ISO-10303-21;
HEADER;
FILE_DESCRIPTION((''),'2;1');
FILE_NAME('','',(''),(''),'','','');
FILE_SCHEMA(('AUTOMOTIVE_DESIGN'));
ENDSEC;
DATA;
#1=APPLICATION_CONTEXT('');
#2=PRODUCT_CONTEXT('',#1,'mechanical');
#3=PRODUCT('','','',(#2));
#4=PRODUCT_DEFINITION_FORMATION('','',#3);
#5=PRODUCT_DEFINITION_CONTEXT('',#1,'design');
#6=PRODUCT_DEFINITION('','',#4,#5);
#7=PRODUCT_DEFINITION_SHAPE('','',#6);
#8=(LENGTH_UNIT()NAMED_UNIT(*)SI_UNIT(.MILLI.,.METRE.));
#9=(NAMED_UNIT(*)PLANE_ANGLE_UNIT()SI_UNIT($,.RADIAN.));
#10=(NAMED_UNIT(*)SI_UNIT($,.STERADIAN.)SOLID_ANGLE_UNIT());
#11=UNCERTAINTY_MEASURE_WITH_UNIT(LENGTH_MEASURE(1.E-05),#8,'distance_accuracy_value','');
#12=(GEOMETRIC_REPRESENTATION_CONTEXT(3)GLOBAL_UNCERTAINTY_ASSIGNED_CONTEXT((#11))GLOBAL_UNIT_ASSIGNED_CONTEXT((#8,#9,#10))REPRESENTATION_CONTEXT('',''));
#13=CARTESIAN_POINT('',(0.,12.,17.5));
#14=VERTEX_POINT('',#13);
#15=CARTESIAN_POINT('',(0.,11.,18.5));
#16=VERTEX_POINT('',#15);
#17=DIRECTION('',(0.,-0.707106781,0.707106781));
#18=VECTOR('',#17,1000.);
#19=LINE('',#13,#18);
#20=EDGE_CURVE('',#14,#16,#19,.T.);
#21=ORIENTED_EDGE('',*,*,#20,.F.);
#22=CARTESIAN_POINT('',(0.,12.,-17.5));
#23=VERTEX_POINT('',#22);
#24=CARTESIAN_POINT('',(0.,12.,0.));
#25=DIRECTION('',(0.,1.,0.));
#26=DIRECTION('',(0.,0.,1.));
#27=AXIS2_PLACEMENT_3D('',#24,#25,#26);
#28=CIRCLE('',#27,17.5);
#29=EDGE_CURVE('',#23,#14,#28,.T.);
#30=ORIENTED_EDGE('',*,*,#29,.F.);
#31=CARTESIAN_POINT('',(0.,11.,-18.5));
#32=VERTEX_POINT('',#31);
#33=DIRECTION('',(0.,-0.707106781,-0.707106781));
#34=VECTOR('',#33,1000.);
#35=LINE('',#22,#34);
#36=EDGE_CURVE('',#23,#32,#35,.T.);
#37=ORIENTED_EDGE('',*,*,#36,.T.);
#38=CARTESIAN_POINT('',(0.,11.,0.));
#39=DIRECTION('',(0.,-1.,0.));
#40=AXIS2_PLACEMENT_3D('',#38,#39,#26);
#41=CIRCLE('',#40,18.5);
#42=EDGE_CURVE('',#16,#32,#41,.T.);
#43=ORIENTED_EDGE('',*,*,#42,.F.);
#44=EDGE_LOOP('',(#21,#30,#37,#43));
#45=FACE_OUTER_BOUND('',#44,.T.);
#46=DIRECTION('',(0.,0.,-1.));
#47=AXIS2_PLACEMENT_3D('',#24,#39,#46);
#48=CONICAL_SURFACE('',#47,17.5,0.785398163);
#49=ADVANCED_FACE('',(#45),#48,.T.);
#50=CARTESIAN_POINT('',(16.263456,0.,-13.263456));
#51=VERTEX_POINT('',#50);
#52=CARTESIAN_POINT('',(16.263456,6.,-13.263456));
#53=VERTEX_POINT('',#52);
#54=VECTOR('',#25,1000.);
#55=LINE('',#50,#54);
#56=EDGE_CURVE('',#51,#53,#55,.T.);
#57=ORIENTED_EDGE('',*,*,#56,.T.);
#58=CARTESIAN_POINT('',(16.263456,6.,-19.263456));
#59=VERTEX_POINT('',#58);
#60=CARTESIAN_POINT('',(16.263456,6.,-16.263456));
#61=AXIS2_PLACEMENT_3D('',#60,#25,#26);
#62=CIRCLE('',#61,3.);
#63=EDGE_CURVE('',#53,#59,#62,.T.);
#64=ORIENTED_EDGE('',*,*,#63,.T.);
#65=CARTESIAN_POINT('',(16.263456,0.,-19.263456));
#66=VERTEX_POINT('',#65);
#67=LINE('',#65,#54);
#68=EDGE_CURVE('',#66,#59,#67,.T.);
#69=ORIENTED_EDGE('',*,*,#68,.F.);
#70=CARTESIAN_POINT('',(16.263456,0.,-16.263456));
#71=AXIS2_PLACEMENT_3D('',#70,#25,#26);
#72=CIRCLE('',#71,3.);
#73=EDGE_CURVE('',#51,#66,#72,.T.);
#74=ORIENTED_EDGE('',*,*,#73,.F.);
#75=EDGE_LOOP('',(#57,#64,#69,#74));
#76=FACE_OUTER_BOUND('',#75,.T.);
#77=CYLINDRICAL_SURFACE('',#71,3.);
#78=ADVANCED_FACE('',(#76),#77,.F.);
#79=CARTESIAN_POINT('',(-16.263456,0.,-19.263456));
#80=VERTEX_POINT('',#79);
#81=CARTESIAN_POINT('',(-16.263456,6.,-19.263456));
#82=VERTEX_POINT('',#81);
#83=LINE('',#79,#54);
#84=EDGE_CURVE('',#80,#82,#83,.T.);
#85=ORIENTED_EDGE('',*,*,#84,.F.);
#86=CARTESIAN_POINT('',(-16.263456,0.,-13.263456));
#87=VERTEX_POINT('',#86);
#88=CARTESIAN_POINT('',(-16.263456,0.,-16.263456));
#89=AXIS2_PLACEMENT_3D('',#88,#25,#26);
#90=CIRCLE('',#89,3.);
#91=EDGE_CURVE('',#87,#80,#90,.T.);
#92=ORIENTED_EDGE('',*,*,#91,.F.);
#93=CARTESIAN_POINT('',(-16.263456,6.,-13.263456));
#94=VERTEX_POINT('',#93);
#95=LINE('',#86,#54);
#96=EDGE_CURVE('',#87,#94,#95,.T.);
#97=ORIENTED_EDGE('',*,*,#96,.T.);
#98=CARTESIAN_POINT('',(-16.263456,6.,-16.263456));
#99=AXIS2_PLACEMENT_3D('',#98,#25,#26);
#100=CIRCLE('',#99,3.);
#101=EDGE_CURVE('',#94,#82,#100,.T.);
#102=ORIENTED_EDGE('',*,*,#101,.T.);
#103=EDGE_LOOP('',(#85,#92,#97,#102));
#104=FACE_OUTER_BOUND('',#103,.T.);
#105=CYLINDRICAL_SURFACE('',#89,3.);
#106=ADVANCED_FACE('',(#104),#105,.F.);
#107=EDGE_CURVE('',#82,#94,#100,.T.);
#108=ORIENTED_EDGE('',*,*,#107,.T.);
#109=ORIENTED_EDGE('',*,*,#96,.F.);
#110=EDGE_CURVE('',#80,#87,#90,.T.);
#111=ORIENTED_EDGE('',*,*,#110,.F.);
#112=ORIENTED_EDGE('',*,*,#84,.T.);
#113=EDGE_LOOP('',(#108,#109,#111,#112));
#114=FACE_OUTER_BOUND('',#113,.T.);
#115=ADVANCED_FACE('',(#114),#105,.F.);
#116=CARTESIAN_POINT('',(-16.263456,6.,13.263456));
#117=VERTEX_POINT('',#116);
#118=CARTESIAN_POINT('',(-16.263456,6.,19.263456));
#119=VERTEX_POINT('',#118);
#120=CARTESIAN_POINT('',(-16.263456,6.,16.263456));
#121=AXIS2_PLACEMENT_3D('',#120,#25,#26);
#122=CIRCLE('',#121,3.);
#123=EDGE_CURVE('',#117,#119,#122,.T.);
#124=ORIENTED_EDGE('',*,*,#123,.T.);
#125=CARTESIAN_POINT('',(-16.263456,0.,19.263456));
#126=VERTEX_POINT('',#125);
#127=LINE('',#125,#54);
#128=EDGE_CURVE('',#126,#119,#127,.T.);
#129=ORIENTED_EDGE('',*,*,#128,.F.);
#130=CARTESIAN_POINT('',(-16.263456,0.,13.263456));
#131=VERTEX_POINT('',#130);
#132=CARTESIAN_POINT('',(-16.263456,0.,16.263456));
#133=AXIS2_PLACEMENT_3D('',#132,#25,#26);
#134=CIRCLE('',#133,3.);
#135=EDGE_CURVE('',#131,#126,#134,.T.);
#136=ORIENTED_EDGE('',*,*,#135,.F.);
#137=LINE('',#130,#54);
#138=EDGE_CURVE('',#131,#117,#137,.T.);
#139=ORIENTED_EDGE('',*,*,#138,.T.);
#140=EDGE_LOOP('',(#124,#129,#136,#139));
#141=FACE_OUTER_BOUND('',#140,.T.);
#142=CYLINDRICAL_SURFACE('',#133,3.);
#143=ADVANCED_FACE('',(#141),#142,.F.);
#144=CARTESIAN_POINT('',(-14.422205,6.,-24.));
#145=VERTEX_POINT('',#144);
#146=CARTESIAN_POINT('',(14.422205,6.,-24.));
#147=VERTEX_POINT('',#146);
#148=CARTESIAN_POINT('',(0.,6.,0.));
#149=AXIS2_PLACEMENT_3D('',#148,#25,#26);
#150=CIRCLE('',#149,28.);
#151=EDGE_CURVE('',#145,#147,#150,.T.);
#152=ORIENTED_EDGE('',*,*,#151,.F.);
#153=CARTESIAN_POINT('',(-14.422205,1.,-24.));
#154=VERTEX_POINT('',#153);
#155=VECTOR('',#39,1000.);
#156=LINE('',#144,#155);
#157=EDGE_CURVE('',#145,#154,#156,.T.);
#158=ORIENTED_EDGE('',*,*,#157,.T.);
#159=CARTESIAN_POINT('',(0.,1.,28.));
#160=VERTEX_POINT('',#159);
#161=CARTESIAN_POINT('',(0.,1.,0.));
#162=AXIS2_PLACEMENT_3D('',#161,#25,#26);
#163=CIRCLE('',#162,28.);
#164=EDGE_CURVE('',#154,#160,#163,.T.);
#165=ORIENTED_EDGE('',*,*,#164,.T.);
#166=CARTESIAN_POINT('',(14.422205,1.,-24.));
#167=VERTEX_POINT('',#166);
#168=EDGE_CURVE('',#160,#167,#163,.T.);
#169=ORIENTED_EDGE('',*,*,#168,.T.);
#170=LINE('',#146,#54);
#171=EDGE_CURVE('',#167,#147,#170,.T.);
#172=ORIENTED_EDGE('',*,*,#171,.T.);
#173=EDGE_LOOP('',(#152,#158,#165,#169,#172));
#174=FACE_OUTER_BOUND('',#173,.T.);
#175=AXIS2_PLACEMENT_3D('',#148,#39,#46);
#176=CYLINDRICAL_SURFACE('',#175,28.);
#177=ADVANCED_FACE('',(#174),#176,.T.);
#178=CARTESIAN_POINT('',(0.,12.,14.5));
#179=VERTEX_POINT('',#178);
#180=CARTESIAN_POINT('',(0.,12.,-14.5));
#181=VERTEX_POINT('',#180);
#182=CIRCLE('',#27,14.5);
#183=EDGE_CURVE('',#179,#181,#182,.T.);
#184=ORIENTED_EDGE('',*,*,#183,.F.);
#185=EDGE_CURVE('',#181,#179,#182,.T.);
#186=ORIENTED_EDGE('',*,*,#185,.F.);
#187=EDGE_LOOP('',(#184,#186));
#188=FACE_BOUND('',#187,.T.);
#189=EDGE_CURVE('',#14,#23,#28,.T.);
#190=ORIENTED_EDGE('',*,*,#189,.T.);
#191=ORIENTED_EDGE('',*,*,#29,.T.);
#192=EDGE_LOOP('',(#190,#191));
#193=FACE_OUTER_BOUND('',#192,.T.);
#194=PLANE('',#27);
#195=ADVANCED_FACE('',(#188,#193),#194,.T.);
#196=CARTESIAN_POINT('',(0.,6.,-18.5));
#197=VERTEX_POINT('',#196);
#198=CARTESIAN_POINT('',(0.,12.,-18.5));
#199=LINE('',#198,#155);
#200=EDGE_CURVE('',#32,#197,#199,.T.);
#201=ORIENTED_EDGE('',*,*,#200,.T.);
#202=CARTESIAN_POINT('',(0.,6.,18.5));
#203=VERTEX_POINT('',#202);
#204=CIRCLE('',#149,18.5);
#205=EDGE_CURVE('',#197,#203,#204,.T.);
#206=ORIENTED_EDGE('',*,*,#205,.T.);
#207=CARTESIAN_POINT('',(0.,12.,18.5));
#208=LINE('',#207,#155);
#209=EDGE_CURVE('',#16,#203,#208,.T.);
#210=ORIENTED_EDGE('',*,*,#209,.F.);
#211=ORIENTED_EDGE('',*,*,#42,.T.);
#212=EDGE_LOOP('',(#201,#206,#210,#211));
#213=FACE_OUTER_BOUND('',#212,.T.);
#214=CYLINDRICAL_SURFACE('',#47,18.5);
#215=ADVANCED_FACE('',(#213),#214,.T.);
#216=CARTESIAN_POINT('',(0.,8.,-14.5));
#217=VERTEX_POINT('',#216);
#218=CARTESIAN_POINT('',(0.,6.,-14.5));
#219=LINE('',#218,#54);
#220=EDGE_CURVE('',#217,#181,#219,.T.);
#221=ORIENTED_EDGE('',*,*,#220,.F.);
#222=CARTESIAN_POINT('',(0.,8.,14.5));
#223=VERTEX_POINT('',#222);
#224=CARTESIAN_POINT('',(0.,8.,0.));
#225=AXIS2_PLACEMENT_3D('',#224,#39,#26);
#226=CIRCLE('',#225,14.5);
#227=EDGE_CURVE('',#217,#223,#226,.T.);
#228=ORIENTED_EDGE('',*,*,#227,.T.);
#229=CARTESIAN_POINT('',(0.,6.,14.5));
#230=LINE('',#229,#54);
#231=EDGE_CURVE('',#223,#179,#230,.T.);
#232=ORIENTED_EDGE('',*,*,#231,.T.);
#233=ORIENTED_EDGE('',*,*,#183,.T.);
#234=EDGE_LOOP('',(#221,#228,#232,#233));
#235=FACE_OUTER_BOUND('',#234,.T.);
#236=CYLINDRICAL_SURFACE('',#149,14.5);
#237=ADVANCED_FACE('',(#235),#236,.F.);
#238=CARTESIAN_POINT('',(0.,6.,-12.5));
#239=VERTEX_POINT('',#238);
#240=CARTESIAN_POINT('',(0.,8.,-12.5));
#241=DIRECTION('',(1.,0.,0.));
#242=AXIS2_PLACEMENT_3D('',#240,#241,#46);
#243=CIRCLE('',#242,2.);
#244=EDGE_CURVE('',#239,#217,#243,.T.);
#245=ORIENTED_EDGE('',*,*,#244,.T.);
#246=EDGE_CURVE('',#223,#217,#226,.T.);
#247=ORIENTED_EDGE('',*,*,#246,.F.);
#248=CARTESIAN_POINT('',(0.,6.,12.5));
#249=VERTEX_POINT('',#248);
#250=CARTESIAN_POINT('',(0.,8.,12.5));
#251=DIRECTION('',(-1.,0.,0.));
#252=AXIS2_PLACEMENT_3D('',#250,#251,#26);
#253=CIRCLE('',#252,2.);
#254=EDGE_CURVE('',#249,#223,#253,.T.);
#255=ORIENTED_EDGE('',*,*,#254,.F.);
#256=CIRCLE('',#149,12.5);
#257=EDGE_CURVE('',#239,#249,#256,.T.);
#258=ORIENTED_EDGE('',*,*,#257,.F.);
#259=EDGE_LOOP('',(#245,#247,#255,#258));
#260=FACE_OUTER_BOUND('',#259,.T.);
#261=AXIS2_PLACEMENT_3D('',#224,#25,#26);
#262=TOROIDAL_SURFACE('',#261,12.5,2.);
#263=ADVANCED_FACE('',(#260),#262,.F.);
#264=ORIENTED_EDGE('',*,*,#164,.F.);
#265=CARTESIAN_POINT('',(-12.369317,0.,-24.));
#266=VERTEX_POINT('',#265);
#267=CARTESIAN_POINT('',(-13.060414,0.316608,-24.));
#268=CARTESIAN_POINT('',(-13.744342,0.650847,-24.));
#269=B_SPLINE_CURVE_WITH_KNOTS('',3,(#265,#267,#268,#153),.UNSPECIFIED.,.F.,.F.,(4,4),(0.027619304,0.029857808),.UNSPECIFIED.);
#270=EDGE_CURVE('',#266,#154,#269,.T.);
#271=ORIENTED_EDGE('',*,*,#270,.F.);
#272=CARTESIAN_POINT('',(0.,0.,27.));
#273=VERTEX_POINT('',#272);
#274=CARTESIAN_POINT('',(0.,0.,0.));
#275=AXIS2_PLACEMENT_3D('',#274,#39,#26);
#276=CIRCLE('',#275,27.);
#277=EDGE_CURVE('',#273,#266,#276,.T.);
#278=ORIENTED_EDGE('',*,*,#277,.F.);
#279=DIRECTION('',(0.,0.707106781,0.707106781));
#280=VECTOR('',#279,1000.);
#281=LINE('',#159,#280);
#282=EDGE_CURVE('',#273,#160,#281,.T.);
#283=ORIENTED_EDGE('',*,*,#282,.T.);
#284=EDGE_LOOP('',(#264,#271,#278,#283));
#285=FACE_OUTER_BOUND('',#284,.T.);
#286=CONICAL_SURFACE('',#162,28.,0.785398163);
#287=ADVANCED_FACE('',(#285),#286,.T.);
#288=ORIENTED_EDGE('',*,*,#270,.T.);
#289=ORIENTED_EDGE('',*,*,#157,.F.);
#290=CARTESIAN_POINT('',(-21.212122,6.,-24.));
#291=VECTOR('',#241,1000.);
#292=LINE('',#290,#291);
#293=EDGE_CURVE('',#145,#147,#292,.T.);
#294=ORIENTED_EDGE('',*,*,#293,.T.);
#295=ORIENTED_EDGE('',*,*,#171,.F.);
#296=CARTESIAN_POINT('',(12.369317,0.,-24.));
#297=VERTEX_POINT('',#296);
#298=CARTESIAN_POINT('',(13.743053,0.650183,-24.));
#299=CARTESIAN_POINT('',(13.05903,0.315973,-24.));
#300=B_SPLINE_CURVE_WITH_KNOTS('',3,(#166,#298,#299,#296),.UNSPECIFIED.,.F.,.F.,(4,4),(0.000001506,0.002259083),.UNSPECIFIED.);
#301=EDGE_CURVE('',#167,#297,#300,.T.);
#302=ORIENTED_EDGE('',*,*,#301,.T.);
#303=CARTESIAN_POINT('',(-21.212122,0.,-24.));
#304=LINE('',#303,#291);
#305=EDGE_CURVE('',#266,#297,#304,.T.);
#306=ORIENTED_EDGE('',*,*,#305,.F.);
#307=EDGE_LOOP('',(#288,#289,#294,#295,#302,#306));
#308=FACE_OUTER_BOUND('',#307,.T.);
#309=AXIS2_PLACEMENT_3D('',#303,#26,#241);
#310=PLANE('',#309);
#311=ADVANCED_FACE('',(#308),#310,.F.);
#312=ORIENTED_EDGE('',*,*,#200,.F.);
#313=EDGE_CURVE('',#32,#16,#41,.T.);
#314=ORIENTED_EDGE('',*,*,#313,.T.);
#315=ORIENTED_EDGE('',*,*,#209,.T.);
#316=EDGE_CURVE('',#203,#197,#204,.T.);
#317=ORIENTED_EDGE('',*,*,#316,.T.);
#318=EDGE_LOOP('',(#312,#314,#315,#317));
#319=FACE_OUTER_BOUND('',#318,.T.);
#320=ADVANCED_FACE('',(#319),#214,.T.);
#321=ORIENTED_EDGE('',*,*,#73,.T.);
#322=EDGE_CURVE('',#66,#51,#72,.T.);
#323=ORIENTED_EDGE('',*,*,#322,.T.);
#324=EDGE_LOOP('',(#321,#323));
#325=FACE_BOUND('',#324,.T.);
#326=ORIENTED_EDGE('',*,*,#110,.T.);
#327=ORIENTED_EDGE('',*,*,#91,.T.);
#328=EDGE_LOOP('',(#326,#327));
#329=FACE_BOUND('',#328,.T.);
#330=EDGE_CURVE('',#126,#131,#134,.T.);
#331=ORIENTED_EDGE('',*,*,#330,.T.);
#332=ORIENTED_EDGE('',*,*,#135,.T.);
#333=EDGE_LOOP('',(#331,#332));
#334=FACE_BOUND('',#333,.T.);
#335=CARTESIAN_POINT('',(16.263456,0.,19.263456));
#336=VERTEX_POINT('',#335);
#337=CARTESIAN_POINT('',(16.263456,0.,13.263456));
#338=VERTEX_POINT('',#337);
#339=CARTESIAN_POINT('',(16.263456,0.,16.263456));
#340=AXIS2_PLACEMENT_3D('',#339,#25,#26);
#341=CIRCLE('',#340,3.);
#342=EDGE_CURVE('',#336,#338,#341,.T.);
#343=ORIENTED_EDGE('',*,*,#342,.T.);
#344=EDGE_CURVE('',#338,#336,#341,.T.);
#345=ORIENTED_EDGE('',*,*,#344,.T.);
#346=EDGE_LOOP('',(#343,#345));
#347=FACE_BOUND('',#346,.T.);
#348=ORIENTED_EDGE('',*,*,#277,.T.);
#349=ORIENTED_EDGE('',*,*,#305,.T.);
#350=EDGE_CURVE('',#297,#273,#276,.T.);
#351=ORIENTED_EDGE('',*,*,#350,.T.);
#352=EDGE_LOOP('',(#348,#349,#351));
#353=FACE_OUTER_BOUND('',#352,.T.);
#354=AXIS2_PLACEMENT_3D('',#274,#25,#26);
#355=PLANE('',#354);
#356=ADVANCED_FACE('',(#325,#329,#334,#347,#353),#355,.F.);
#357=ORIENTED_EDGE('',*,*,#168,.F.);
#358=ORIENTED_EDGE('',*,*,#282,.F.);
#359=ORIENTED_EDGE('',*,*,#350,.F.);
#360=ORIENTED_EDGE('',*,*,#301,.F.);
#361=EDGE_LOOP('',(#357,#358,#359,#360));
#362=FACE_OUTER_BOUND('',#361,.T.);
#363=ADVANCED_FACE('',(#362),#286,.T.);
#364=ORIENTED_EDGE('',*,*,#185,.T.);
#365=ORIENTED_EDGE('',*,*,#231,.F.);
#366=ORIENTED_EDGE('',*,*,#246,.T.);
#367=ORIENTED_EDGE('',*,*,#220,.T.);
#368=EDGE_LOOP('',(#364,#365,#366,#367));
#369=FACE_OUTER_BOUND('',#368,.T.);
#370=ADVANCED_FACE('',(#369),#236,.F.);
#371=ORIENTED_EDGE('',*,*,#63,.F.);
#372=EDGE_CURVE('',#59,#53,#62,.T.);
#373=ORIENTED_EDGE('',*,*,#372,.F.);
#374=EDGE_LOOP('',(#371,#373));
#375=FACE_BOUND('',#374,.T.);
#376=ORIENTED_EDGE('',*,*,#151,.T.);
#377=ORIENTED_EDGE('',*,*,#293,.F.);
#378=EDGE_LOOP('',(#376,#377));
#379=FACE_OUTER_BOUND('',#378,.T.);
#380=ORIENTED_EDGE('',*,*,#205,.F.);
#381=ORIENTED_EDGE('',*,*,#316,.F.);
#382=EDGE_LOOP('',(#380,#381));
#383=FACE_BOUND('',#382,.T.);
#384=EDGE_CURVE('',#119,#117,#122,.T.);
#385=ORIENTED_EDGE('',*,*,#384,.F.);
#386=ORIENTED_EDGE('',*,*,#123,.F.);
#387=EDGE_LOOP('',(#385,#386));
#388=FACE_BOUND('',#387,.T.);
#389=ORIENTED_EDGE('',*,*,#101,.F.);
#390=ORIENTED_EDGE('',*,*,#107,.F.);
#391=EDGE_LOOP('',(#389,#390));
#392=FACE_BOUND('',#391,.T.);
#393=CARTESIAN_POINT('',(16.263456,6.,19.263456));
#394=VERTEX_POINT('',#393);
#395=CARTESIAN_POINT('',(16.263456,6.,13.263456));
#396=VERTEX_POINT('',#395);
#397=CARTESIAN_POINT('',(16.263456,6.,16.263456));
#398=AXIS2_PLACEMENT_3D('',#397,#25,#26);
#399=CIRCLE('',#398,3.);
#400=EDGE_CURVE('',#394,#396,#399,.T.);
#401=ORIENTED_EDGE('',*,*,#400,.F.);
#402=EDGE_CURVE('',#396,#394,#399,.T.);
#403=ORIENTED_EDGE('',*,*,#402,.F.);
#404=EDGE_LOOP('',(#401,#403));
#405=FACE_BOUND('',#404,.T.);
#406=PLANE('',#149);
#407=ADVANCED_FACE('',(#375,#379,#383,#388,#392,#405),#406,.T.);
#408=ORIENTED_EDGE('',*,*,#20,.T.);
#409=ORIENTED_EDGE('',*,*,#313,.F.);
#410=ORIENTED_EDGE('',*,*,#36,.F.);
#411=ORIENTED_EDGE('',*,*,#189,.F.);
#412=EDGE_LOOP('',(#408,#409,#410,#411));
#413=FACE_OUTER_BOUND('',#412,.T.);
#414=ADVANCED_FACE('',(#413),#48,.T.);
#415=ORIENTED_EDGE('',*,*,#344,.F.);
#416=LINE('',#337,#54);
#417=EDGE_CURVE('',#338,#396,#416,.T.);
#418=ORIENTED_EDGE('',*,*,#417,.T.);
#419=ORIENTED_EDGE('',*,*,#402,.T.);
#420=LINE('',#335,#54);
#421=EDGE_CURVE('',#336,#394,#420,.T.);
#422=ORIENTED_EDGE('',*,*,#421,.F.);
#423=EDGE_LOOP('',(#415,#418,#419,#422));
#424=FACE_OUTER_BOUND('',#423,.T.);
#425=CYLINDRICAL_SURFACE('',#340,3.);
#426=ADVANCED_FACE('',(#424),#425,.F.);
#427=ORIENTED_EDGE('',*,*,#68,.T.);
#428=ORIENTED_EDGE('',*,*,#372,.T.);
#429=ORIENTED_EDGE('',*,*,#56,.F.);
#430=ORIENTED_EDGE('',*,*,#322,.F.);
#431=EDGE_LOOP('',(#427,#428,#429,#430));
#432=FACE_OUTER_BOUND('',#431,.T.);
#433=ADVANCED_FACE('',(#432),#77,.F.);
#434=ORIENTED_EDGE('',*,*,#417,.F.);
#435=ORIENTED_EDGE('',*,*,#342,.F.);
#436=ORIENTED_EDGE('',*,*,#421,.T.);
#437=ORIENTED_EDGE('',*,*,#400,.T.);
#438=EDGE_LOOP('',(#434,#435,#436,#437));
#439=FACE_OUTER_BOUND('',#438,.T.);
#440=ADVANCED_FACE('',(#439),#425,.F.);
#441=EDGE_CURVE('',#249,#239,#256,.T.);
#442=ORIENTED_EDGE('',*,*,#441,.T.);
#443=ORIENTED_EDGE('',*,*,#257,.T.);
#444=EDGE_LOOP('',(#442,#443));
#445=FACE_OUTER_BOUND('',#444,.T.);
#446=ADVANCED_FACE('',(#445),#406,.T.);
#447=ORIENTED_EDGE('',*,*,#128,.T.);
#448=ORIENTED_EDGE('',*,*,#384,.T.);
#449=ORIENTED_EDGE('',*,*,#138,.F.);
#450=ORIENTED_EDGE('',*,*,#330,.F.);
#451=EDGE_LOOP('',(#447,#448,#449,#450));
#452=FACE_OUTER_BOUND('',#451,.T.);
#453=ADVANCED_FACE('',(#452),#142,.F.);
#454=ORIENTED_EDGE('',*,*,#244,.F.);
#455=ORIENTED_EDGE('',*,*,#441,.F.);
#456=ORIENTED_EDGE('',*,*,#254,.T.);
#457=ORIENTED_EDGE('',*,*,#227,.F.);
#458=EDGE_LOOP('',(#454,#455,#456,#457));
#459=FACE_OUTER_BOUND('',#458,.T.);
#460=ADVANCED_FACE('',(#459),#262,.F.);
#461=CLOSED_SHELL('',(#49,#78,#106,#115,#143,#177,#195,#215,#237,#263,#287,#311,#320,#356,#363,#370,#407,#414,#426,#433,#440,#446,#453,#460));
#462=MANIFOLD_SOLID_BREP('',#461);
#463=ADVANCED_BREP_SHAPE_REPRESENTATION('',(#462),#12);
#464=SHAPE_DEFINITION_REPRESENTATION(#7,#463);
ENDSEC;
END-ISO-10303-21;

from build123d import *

# Parameters (mm, degrees)
SKETCH1_R           = 28
BOSS_EXTRUDE1_DEPTH = 6
SKETCH2_R           = 18.5
BOSS_EXTRUDE2_DEPTH = 6
SKETCH3_R           = 14.5
CUT_EXTRUDE1_DEPTH  = 6
FILLET2_R           = 2
CHAMFER1_SIZE       = 1
SKETCH4_R           = 3
CUT_EXTRUDE2_DEPTH  = 6
SKETCH5_W           = 48.146036261
SKETCH5_H           = 7.706921361
CUT_EXTRUDE3_DEPTH  = 6


with BuildPart() as part:
    # Sketch1 → Boss-Extrude1 (new body)
    with BuildSketch(Plane(origin=(0, 0, 0), x_dir=(1, 0, 0), z_dir=(0, 1, 0))):
        with Locations(Location((0, 0, 0), (0, 0, 270))):
            Circle(SKETCH1_R)
    extrude(amount=BOSS_EXTRUDE1_DEPTH)

    # Sketch2 → Boss-Extrude2 (add)
    with BuildSketch(Plane(origin=(0, 6, 0), x_dir=(1, 0, 0), z_dir=(0, 1, 0))):
        with Locations(Location((0, 0, 0), (0, 0, 270))):
            Circle(SKETCH2_R)
    extrude(amount=BOSS_EXTRUDE2_DEPTH)

    # Sketch3 → Cut-Extrude1 (cut)
    with BuildSketch(Plane(origin=(0, 12, 0), x_dir=(1, 0, 0), z_dir=(0, 1, 0))):
        with Locations(Location((0, 0, 0), (0, 0, 270))):
            Circle(SKETCH3_R)
    extrude(amount=-CUT_EXTRUDE1_DEPTH, mode=Mode.SUBTRACT)

    # Fillet2
    fillet2_edges = [part.edges().sort_by_distance(p)[0] for p in [
        (0, 6, -14.5),
    ]]
    fillet(fillet2_edges, radius=FILLET2_R)

    # Chamfer1
    chamfer1_edges = [part.edges().sort_by_distance(p)[0] for p in [
        (0, 0, -28),
        (0, 12, -18.5),
    ]]
    chamfer(chamfer1_edges, length=CHAMFER1_SIZE)

    # Sketch4 → Cut-Extrude2 (cut)
    with BuildSketch(Plane(origin=(0, 6, 0), x_dir=(1, 0, 0), z_dir=(0, 1, 0))):
        with Locations(Location((-16.263455967, 16.263455967, 0), (0, 0, 270))):
            Circle(SKETCH4_R)
        with Locations(Location((16.263455967, 16.263455967, 0), (0, 0, 270))):
            Circle(SKETCH4_R)
        with Locations(Location((16.263455967, -16.263455967, 0), (0, 0, 270))):
            Circle(SKETCH4_R)
        with Locations(Location((-16.263455967, -16.263455967, 0), (0, 0, 270))):
            Circle(SKETCH4_R)
    extrude(amount=-CUT_EXTRUDE2_DEPTH, mode=Mode.SUBTRACT)

    # Sketch5 → Cut-Extrude3 (cut)
    with BuildSketch(Plane(origin=(0, 6, 0), x_dir=(1, 0, 0), z_dir=(0, 1, 0))):
        with Locations((2.860896385, 27.85346068)):
            Rectangle(SKETCH5_W, SKETCH5_H)
    extrude(amount=-CUT_EXTRUDE3_DEPTH, mode=Mode.SUBTRACT)


solid = part.part
